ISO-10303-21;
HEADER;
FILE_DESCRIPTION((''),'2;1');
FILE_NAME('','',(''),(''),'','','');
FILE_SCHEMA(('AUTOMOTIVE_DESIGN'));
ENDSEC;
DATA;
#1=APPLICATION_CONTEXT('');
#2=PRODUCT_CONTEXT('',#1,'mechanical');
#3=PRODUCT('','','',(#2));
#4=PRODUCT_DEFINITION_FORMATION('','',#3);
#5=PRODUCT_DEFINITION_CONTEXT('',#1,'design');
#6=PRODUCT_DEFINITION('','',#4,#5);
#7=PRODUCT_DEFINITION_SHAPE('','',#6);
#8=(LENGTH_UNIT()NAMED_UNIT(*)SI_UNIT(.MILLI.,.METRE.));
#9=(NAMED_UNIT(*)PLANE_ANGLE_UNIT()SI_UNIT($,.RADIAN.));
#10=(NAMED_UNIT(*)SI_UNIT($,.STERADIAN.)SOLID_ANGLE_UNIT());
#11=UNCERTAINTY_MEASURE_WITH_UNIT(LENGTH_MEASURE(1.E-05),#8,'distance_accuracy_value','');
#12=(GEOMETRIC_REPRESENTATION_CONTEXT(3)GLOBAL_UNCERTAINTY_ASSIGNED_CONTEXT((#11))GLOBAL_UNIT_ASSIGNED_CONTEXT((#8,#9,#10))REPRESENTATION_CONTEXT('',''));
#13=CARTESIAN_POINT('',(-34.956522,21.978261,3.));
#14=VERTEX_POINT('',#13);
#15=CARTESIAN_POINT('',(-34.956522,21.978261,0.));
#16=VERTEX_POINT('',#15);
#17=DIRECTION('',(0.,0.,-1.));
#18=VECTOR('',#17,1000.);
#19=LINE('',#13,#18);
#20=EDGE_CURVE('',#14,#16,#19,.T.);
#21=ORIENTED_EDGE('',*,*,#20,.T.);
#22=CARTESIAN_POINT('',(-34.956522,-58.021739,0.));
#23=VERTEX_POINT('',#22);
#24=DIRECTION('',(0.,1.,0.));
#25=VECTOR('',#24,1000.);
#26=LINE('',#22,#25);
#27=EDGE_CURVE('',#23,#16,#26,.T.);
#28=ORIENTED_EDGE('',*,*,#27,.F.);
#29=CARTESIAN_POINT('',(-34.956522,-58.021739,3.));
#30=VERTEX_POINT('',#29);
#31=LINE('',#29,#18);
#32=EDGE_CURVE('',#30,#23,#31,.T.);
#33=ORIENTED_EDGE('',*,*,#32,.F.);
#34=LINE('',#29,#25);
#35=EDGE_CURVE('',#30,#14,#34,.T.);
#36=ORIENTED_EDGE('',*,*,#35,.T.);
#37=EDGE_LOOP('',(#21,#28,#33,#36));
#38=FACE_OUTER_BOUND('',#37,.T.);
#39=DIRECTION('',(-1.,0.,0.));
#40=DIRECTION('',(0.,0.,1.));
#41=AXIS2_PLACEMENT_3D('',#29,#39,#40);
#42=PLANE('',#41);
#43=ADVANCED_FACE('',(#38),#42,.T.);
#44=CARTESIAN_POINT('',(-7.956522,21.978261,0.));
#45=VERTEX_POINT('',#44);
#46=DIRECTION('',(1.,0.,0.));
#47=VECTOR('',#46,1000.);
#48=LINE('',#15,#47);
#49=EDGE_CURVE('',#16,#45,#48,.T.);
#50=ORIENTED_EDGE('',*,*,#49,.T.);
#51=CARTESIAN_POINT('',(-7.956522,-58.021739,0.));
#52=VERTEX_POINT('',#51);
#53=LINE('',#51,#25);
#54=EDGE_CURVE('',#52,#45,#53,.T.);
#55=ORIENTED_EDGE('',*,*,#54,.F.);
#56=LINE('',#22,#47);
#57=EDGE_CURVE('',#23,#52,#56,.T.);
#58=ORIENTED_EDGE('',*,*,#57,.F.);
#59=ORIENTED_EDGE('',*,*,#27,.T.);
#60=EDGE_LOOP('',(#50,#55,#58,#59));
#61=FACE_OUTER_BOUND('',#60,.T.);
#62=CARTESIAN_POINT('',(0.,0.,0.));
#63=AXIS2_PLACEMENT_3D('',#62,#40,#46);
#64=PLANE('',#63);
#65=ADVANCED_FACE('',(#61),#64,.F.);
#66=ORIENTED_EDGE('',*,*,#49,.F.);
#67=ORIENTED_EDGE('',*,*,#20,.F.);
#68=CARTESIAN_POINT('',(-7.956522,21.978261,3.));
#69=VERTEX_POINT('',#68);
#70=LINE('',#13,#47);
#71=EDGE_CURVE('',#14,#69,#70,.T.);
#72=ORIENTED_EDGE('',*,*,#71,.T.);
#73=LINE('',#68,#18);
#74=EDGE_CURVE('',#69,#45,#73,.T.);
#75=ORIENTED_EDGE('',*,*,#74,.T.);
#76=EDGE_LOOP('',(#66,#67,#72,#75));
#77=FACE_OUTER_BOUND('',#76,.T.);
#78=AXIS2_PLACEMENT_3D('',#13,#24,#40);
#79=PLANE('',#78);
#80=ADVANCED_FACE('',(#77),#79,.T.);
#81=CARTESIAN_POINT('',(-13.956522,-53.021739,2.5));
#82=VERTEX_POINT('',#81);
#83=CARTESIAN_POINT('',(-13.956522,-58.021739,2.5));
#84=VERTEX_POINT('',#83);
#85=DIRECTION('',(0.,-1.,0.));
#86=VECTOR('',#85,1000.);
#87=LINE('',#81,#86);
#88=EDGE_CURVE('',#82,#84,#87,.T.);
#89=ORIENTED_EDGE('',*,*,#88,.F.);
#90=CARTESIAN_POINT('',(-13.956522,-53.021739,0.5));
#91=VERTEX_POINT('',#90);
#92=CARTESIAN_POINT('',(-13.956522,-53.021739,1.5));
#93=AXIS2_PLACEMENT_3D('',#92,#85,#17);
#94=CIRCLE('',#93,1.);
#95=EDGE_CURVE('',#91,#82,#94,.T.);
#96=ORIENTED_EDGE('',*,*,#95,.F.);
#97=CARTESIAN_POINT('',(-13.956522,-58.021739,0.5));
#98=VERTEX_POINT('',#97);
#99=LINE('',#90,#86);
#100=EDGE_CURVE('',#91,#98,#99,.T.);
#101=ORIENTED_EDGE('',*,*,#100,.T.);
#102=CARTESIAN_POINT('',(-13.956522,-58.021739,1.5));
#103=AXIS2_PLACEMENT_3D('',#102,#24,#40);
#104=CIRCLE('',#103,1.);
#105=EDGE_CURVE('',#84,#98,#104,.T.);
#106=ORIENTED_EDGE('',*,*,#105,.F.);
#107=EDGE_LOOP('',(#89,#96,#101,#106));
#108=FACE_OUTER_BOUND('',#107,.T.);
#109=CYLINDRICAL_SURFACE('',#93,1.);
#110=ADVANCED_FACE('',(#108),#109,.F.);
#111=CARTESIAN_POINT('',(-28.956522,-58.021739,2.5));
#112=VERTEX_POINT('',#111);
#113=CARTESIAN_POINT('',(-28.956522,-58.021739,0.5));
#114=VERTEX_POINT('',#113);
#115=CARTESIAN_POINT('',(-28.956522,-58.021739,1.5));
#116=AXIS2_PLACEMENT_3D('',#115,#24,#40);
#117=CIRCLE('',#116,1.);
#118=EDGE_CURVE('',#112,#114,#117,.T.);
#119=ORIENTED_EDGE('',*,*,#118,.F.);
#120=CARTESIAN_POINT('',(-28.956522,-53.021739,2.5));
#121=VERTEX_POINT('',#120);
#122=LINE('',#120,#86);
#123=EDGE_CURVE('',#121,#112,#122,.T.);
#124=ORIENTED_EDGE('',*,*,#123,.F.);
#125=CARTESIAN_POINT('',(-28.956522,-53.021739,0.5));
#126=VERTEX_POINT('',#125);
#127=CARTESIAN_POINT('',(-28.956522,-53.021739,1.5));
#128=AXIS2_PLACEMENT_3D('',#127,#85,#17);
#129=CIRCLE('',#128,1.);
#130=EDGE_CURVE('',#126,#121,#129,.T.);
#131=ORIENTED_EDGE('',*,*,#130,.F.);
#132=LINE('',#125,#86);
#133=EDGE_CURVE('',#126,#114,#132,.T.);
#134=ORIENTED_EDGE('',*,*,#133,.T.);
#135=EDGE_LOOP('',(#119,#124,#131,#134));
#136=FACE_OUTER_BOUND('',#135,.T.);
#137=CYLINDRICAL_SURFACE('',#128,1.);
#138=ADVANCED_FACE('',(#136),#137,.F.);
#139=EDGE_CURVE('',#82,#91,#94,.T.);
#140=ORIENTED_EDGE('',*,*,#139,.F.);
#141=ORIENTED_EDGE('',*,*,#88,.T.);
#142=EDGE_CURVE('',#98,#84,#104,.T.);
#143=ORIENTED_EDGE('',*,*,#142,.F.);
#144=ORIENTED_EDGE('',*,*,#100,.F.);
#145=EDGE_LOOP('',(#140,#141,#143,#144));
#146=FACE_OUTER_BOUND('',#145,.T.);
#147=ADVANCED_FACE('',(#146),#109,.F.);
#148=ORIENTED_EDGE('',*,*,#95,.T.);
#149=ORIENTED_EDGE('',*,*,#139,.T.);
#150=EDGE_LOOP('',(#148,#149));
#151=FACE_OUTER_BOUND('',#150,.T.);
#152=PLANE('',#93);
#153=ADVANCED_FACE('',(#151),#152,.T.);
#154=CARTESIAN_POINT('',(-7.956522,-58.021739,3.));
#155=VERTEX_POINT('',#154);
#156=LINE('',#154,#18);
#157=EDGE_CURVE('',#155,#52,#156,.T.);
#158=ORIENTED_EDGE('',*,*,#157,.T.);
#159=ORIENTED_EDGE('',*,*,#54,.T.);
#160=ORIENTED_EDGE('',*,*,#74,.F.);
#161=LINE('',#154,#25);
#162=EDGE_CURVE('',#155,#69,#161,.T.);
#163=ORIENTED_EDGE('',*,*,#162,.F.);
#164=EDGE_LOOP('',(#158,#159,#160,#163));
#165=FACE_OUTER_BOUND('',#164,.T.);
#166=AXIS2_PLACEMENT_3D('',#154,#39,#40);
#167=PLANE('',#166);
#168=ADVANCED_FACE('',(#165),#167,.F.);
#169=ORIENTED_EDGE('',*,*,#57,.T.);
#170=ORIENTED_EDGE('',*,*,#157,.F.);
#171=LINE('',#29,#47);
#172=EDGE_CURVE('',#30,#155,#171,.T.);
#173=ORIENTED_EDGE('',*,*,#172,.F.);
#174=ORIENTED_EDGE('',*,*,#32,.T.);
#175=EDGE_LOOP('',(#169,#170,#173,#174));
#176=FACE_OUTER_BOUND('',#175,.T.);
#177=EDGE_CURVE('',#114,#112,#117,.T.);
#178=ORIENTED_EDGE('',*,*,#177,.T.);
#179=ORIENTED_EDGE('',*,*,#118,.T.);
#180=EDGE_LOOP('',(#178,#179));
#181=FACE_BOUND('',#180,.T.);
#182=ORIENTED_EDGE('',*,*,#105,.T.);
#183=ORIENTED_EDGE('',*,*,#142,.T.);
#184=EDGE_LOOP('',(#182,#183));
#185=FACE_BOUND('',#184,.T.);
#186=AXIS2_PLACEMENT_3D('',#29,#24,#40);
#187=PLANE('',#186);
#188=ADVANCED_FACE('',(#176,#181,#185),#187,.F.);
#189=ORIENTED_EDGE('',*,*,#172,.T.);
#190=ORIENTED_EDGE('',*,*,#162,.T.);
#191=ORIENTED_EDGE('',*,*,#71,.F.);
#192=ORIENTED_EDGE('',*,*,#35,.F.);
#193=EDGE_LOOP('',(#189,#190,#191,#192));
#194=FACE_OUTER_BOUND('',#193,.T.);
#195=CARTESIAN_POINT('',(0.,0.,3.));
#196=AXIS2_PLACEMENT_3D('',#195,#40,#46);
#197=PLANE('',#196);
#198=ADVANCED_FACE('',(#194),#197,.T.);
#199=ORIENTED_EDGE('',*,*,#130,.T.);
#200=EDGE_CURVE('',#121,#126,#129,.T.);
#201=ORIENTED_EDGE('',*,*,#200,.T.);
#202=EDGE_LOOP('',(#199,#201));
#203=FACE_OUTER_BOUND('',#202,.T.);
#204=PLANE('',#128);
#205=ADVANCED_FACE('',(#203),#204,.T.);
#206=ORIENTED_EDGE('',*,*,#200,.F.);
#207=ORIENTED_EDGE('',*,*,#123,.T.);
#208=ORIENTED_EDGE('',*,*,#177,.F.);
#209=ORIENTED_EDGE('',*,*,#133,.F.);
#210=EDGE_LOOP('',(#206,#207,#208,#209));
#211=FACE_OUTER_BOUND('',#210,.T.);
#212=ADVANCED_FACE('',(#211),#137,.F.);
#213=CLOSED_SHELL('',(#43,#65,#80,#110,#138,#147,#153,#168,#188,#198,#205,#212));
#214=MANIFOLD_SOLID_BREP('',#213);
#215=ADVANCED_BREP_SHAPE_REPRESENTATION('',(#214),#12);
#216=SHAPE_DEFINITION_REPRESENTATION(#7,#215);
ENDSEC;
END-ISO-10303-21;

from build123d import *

# Parameters (mm, degrees)
SKETCH_1_W          = 27
SKETCH_1_H          = 80
EXTRUDE_2_DEPTH     = 3
SKETCH_2_R          = 1
CUT_EXTRUDE_1_DEPTH = 15


with BuildPart() as part:
    # 草图1 → 凸台-拉伸2 (new body)
    with BuildSketch(Plane.XY):
        with Locations((-21.456521739, -18.02173913)):
            Rectangle(SKETCH_1_W, SKETCH_1_H)
    extrude(amount=EXTRUDE_2_DEPTH)

    # 草图2 → 切除-拉伸1 (cut)
    with BuildSketch(Plane(origin=(820.104098161, -68.02173913, 1111.231170435), x_dir=(-0.9925461516413246, -2.2389179114641602e-14, -0.12186934340512692), z_dir=(0, -1, 0))):
        with Locations(Location((963.085867609, 999.8129825, 0), (0, 0, 83))):
            Circle(SKETCH_2_R)
        with Locations(Location((977.974059883, 997.984942349, 0), (0, 0, 83))):
            Circle(SKETCH_2_R)
        with Locations((961.501566145, 986.909882529)):
            Circle(SKETCH_2_R)
        with Locations((976.389758419, 985.081842378)):
            Circle(SKETCH_2_R)
    extrude(amount=-CUT_EXTRUDE_1_DEPTH, mode=Mode.SUBTRACT)


solid = part.part
